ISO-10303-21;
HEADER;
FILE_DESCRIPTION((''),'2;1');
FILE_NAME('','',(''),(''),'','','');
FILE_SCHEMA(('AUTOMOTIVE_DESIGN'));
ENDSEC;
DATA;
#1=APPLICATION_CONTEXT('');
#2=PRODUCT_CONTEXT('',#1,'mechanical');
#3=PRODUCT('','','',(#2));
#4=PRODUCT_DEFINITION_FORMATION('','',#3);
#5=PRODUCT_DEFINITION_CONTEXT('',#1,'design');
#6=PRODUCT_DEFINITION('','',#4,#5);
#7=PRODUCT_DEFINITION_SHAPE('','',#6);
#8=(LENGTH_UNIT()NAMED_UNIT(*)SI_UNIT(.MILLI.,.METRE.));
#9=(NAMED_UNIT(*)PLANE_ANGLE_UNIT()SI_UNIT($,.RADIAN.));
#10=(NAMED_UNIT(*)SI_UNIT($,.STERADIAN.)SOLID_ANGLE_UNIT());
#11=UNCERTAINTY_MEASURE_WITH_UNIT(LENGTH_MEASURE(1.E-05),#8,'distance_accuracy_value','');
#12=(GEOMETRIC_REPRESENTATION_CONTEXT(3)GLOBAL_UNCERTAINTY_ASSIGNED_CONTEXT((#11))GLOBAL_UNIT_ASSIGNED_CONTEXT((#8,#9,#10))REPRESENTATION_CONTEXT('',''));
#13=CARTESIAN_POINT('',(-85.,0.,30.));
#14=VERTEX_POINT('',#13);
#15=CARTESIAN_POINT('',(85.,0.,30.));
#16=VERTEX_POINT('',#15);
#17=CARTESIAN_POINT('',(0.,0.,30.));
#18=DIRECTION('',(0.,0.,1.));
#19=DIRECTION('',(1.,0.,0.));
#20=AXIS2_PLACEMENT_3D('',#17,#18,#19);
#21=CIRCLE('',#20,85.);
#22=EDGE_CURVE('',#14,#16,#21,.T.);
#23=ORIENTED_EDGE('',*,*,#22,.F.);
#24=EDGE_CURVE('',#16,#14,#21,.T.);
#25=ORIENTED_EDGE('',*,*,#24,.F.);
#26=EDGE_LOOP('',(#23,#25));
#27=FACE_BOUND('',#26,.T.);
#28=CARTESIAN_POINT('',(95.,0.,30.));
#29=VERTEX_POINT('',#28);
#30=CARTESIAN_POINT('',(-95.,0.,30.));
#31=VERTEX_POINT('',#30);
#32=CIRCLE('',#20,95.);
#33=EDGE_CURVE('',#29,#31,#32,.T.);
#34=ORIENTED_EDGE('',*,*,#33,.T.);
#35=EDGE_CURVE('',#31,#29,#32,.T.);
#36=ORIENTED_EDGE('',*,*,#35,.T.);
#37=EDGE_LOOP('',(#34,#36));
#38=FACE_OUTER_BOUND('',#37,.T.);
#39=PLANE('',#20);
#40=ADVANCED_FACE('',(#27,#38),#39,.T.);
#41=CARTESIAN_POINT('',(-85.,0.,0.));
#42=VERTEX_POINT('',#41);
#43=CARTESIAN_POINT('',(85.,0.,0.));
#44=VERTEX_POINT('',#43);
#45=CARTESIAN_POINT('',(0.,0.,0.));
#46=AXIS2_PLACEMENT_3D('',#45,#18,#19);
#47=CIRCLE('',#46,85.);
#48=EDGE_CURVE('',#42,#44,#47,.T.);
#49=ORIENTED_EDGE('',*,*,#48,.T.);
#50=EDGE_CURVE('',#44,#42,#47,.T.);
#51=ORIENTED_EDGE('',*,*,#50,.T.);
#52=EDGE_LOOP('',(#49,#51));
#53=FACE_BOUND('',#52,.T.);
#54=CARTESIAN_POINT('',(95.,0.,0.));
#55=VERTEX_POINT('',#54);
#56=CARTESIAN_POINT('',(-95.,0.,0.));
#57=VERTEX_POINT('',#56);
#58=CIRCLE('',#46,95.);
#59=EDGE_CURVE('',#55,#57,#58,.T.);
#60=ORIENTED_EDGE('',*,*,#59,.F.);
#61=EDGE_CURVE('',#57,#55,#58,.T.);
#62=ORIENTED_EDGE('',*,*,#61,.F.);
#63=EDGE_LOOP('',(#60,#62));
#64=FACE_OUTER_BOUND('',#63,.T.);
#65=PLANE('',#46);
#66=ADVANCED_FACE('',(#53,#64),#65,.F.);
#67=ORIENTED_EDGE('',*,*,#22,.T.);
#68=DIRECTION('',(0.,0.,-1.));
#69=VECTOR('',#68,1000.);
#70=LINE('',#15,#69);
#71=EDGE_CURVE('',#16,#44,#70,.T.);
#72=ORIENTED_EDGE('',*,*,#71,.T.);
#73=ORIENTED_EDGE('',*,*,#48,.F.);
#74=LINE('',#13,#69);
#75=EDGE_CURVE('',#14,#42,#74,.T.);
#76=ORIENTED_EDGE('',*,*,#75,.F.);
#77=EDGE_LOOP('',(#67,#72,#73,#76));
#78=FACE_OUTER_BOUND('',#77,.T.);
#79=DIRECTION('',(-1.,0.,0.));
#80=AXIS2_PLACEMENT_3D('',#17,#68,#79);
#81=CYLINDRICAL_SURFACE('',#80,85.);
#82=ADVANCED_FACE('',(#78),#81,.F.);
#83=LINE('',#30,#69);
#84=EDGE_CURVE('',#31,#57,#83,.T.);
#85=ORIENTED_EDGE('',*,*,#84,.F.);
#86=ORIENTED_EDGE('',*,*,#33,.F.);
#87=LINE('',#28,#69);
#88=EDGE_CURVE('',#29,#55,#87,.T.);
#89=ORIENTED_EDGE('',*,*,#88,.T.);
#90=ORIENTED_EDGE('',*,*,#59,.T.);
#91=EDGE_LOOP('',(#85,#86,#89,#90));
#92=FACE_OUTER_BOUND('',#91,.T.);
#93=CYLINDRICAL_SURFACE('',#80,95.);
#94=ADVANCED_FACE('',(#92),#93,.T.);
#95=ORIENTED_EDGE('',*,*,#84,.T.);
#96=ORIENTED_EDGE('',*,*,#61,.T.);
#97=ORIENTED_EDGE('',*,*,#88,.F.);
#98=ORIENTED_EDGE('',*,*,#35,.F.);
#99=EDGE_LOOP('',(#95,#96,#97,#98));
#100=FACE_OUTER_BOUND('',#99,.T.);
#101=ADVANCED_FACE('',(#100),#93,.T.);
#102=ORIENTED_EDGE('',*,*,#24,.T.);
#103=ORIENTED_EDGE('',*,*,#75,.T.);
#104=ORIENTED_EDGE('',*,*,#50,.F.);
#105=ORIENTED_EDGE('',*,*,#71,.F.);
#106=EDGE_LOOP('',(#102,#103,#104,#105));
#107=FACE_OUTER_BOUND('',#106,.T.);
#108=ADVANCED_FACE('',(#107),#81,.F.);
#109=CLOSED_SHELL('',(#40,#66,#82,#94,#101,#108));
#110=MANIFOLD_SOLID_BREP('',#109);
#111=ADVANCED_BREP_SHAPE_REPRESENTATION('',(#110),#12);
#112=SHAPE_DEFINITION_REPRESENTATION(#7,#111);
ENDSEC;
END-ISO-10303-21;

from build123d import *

# Parameters (mm, degrees)
SKETCH2_R           = 95
SKETCH2_R_2         = 85
BOSS_EXTRUDE1_DEPTH = 30


with BuildPart() as part:
    # Sketch2 → Boss-Extrude1 (new body)
    with BuildSketch(Plane.XY):
        Circle(SKETCH2_R)
        Circle(SKETCH2_R_2, mode=Mode.SUBTRACT)
    extrude(amount=BOSS_EXTRUDE1_DEPTH)


solid = part.part
